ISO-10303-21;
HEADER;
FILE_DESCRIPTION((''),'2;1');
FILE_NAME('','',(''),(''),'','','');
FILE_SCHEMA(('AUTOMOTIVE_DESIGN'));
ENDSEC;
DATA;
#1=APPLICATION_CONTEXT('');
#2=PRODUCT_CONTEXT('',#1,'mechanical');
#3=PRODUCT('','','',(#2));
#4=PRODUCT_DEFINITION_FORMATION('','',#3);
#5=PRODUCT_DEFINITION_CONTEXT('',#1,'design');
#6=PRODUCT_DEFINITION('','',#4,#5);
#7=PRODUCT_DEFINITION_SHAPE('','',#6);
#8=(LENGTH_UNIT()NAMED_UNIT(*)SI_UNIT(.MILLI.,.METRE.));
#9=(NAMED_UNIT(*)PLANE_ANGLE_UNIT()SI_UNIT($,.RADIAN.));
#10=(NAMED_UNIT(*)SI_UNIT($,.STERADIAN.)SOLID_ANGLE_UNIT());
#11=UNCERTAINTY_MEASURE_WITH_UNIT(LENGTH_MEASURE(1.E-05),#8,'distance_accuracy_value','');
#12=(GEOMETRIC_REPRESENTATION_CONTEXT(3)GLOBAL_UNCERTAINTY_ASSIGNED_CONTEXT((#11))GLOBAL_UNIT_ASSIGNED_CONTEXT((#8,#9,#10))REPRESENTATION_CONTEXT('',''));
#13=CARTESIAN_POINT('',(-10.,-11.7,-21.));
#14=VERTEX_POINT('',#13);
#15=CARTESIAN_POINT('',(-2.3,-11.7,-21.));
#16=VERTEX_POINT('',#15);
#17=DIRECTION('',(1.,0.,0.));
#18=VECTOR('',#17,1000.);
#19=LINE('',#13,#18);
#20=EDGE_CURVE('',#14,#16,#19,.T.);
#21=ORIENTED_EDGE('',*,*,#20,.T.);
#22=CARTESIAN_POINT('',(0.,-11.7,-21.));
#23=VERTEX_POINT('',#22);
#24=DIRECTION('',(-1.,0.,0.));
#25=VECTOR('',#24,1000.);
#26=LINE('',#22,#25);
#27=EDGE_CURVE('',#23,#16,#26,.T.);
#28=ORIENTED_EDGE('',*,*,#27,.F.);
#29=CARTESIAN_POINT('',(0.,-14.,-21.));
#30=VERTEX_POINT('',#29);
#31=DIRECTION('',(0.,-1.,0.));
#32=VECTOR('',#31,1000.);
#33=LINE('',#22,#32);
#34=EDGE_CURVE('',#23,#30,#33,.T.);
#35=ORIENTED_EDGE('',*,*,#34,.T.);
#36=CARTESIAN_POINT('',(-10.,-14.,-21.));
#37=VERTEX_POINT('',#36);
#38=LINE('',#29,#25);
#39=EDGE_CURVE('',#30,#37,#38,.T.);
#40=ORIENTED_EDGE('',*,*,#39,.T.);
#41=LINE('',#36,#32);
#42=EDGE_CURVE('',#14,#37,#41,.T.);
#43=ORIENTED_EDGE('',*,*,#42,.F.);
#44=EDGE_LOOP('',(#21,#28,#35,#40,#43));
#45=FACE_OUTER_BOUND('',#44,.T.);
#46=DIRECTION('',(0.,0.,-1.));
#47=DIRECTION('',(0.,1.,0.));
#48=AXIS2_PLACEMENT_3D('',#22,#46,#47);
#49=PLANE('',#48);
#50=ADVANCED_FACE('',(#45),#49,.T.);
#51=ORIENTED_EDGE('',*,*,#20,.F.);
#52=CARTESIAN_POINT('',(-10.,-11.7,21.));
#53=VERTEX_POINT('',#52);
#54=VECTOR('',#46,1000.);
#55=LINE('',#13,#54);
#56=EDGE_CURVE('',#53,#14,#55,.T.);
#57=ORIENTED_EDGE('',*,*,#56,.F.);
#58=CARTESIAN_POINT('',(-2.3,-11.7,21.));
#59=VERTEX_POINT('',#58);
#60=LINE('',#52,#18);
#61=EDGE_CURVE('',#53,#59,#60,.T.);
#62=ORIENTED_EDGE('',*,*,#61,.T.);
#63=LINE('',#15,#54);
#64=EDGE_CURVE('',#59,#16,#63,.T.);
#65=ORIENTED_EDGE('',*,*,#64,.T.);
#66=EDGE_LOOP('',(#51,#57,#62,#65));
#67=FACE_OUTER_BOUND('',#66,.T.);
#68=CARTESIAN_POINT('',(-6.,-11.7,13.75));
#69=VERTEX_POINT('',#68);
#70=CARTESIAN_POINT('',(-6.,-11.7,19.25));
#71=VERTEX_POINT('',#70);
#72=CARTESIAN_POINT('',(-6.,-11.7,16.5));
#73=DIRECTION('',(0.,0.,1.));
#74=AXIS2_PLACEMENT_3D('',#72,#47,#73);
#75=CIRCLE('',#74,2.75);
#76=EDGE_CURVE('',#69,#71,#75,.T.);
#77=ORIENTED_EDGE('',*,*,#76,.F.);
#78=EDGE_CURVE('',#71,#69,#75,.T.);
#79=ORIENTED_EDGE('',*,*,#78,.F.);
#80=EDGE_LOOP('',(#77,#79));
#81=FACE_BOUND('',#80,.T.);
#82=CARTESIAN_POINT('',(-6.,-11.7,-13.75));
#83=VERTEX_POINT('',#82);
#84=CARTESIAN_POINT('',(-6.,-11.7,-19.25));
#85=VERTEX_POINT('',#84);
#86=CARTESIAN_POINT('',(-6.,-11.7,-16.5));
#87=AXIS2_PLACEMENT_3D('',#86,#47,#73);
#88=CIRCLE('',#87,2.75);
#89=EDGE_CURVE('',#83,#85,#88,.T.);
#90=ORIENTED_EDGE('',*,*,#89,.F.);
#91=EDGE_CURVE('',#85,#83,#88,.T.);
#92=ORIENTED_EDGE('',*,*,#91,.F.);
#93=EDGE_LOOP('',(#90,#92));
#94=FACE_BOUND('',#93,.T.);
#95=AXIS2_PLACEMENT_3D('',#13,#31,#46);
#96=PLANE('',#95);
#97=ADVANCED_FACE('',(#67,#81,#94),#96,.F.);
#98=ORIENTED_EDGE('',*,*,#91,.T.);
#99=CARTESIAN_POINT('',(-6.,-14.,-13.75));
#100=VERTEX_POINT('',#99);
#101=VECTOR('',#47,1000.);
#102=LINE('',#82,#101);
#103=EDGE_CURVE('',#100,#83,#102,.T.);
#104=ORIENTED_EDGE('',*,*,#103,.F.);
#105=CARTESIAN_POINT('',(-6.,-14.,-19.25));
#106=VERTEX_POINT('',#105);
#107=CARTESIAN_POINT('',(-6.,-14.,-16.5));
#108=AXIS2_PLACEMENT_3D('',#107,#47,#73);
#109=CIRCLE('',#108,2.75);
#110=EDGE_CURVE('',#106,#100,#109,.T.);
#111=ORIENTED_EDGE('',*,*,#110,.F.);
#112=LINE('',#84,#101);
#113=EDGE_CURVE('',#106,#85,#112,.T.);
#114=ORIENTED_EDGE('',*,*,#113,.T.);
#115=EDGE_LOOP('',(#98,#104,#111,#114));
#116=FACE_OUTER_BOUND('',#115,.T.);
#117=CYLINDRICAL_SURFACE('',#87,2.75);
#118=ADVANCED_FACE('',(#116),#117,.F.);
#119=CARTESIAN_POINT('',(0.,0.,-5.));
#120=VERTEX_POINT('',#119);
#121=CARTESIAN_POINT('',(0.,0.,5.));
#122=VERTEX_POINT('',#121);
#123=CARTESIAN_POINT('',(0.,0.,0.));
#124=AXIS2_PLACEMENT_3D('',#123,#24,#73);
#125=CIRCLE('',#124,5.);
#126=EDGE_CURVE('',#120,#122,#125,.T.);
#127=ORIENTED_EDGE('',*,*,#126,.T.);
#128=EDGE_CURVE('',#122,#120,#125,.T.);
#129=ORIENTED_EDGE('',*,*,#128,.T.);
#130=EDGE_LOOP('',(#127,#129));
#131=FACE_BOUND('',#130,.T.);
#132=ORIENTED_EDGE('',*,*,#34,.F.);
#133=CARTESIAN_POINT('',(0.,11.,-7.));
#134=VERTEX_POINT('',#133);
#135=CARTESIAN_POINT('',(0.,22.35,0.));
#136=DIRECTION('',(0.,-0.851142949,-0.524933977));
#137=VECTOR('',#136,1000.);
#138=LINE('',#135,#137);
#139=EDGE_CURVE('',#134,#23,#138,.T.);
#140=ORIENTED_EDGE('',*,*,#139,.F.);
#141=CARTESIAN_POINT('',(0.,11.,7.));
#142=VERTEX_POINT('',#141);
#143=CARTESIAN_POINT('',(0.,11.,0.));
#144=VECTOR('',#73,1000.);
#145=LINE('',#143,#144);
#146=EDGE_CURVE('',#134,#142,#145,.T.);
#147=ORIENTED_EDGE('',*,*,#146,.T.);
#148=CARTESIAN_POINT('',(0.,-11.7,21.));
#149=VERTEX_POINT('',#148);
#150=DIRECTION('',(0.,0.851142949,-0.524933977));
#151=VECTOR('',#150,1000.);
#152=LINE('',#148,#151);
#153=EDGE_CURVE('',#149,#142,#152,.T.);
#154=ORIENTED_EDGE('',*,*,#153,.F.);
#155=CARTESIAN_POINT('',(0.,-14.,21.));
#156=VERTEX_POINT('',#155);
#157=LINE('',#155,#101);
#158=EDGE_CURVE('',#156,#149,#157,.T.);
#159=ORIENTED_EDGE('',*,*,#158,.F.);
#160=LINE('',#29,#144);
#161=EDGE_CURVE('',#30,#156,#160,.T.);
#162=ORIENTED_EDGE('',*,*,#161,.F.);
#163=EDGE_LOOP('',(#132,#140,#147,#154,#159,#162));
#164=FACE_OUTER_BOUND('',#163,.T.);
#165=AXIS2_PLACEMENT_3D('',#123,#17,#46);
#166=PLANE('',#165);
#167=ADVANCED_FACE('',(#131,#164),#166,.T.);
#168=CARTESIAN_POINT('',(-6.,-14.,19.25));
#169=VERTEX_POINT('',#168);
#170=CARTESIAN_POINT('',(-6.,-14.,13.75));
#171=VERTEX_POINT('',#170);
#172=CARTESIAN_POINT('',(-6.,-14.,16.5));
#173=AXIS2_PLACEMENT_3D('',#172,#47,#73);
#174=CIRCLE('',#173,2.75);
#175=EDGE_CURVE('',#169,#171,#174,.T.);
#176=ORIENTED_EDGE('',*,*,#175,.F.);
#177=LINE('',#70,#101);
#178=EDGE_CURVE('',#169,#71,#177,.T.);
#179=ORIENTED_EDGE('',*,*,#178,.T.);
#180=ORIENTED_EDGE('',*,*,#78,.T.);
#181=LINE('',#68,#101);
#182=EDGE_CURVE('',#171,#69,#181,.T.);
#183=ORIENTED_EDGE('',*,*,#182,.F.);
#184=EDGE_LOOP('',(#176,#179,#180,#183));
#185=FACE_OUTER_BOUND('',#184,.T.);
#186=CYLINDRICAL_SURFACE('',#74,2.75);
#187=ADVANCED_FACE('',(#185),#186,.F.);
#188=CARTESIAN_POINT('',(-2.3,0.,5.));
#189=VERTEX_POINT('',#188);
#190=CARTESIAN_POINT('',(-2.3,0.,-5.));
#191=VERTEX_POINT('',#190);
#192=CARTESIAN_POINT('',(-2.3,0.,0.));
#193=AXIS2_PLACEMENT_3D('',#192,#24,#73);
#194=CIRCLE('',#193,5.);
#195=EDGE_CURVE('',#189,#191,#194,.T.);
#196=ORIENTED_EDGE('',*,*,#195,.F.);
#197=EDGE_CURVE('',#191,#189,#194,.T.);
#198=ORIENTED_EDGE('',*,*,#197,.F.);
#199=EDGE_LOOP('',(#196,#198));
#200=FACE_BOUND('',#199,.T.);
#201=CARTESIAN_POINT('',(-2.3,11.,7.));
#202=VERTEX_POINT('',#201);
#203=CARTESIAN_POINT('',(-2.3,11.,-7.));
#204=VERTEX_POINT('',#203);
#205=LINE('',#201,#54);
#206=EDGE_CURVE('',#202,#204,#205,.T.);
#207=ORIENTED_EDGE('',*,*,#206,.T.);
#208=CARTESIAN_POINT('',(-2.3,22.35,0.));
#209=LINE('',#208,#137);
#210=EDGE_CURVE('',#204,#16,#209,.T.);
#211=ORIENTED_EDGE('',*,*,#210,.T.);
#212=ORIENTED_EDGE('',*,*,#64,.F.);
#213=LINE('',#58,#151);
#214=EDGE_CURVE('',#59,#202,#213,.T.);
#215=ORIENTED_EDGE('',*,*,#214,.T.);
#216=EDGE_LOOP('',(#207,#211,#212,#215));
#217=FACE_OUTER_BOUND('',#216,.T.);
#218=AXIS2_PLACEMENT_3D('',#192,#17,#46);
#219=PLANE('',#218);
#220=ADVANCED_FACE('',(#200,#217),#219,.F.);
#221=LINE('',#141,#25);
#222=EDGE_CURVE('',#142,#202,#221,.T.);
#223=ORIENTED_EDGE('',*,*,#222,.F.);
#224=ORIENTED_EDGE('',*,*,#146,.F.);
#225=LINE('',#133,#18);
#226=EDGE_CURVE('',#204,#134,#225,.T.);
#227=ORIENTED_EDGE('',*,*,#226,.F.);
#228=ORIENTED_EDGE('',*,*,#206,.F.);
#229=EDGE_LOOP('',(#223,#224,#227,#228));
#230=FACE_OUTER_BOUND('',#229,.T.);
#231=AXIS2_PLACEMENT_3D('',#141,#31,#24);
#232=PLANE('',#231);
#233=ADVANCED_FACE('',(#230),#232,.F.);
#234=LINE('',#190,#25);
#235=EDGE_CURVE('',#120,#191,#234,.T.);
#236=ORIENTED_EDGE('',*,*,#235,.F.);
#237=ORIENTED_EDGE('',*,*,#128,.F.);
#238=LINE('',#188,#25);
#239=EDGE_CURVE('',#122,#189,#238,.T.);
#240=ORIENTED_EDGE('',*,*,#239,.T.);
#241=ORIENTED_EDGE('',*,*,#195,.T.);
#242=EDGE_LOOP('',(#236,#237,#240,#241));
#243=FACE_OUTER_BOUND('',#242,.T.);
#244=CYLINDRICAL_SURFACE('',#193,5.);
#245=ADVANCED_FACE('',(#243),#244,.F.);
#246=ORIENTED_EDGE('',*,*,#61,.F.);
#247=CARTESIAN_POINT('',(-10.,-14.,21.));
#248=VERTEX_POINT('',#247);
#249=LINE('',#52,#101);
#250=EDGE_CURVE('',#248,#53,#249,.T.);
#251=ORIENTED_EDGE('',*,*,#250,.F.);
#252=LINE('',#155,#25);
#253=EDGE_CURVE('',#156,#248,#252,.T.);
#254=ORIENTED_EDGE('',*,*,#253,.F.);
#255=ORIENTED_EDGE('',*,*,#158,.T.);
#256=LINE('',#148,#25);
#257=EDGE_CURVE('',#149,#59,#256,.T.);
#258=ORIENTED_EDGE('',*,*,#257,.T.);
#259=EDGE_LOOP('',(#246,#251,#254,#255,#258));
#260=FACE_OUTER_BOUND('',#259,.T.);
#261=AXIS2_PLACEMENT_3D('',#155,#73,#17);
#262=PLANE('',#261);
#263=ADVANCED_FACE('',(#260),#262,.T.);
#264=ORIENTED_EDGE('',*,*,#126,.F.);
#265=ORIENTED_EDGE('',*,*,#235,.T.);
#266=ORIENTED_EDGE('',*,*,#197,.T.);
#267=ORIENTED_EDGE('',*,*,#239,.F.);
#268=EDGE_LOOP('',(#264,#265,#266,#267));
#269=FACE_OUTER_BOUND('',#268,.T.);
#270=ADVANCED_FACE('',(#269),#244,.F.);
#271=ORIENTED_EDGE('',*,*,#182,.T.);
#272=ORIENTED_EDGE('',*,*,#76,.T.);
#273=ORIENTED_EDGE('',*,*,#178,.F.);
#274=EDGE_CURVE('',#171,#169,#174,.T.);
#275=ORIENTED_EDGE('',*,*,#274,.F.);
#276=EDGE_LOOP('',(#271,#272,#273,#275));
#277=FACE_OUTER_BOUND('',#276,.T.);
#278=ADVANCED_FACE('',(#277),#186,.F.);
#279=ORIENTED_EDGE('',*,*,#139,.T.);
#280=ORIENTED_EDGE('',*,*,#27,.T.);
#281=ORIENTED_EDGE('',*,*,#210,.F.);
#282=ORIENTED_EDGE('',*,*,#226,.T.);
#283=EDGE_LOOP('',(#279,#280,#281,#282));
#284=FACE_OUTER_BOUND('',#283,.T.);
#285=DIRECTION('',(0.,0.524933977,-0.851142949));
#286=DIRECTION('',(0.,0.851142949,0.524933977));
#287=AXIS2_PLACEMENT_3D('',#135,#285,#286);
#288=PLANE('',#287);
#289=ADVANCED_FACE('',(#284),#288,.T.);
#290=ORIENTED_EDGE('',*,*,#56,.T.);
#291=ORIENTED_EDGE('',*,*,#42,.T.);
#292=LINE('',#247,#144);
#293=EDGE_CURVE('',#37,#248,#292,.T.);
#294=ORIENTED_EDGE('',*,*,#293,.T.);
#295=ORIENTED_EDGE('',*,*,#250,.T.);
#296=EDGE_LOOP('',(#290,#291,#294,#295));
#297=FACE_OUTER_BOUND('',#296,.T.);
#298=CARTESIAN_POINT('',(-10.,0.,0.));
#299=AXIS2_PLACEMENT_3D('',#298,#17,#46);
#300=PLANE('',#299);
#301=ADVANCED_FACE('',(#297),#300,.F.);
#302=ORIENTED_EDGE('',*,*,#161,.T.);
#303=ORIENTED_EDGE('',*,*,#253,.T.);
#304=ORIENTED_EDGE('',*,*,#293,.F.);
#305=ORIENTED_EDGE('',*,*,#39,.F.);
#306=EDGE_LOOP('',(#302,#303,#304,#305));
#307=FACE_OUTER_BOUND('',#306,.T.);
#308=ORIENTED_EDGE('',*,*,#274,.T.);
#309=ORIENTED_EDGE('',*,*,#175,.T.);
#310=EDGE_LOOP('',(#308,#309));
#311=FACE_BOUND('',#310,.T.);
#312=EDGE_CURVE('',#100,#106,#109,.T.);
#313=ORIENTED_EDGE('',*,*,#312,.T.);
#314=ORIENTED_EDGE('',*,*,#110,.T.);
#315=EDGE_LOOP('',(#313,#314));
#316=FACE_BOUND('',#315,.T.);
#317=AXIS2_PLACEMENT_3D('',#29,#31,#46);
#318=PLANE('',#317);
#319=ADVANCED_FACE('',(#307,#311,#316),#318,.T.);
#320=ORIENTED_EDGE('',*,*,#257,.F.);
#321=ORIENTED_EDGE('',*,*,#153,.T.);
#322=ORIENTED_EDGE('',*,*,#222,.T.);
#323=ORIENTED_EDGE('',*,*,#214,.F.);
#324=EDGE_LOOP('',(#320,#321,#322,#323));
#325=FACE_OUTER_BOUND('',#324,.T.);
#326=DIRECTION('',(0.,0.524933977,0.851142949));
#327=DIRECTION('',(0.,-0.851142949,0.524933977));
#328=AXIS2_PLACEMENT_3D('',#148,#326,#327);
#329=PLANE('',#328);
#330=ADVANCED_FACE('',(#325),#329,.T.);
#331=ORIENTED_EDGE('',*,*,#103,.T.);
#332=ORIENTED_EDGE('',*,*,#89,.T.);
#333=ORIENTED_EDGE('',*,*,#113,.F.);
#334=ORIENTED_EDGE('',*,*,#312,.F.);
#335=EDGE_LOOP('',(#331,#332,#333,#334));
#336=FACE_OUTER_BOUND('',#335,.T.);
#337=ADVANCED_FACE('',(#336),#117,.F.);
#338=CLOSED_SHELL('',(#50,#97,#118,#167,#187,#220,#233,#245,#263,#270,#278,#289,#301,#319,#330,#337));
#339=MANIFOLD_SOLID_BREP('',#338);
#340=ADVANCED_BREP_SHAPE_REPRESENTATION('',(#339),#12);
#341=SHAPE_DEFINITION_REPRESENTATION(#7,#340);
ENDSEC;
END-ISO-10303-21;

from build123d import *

# Parameters (mm, degrees)
BOSS_EXTRUDE1_DEPTH        = 2.3
SKETCH2_W                  = 42
SKETCH2_H                  = 2.3
BOSS_EXTRUDE2_DEPTH        = 7.7
F_10_0_10_DIAMETER_HOLE1_D = 10
F_5_5_5_5_DIAMETER_HOLE1_D = 5.5
CHAMFER1_SIZE              = 13.335010311


with BuildPart() as part:
    # Sketch1 → Boss-Extrude1 (new body)
    with BuildSketch(Plane(origin=(-2.3, 0, 0), x_dir=(0, -1, 0), z_dir=(-1, 0, 0))):
        Polygon((11.7, 21), (-22.35, 0), (11.7, -21), (14, -21), (14, 21), align=None)
    extrude(amount=-BOSS_EXTRUDE1_DEPTH)

    # Sketch2 → Boss-Extrude2 (add)
    with BuildSketch(Plane.ZY.offset(2.3)):
        with Locations((0, -12.85)):
            Rectangle(SKETCH2_W, SKETCH2_H)
    extrude(amount=BOSS_EXTRUDE2_DEPTH)

    # Ø10.0 (10) Diameter Hole1 (through all)
    with Locations(Plane.ZY.offset(2.3)):
        with Locations((0, 0)):
            Hole(F_10_0_10_DIAMETER_HOLE1_D / 2)

    # Ø5.5 (5.5) Diameter Hole1 (through all)
    with Locations(Plane(origin=(0, -11.7, 0), x_dir=(1, 0, 0), z_dir=(0, 1, 0))):
        with Locations((-6, -16.5), (-6, 16.5)):
            Hole(F_5_5_5_5_DIAMETER_HOLE1_D / 2)

    # Chamfer1
    chamfer1_edges = [part.edges().sort_by_distance(p)[0] for p in [
        (-1.15, 22.35, 0),
    ]]
    chamfer(chamfer1_edges, length=CHAMFER1_SIZE)


solid = part.part
